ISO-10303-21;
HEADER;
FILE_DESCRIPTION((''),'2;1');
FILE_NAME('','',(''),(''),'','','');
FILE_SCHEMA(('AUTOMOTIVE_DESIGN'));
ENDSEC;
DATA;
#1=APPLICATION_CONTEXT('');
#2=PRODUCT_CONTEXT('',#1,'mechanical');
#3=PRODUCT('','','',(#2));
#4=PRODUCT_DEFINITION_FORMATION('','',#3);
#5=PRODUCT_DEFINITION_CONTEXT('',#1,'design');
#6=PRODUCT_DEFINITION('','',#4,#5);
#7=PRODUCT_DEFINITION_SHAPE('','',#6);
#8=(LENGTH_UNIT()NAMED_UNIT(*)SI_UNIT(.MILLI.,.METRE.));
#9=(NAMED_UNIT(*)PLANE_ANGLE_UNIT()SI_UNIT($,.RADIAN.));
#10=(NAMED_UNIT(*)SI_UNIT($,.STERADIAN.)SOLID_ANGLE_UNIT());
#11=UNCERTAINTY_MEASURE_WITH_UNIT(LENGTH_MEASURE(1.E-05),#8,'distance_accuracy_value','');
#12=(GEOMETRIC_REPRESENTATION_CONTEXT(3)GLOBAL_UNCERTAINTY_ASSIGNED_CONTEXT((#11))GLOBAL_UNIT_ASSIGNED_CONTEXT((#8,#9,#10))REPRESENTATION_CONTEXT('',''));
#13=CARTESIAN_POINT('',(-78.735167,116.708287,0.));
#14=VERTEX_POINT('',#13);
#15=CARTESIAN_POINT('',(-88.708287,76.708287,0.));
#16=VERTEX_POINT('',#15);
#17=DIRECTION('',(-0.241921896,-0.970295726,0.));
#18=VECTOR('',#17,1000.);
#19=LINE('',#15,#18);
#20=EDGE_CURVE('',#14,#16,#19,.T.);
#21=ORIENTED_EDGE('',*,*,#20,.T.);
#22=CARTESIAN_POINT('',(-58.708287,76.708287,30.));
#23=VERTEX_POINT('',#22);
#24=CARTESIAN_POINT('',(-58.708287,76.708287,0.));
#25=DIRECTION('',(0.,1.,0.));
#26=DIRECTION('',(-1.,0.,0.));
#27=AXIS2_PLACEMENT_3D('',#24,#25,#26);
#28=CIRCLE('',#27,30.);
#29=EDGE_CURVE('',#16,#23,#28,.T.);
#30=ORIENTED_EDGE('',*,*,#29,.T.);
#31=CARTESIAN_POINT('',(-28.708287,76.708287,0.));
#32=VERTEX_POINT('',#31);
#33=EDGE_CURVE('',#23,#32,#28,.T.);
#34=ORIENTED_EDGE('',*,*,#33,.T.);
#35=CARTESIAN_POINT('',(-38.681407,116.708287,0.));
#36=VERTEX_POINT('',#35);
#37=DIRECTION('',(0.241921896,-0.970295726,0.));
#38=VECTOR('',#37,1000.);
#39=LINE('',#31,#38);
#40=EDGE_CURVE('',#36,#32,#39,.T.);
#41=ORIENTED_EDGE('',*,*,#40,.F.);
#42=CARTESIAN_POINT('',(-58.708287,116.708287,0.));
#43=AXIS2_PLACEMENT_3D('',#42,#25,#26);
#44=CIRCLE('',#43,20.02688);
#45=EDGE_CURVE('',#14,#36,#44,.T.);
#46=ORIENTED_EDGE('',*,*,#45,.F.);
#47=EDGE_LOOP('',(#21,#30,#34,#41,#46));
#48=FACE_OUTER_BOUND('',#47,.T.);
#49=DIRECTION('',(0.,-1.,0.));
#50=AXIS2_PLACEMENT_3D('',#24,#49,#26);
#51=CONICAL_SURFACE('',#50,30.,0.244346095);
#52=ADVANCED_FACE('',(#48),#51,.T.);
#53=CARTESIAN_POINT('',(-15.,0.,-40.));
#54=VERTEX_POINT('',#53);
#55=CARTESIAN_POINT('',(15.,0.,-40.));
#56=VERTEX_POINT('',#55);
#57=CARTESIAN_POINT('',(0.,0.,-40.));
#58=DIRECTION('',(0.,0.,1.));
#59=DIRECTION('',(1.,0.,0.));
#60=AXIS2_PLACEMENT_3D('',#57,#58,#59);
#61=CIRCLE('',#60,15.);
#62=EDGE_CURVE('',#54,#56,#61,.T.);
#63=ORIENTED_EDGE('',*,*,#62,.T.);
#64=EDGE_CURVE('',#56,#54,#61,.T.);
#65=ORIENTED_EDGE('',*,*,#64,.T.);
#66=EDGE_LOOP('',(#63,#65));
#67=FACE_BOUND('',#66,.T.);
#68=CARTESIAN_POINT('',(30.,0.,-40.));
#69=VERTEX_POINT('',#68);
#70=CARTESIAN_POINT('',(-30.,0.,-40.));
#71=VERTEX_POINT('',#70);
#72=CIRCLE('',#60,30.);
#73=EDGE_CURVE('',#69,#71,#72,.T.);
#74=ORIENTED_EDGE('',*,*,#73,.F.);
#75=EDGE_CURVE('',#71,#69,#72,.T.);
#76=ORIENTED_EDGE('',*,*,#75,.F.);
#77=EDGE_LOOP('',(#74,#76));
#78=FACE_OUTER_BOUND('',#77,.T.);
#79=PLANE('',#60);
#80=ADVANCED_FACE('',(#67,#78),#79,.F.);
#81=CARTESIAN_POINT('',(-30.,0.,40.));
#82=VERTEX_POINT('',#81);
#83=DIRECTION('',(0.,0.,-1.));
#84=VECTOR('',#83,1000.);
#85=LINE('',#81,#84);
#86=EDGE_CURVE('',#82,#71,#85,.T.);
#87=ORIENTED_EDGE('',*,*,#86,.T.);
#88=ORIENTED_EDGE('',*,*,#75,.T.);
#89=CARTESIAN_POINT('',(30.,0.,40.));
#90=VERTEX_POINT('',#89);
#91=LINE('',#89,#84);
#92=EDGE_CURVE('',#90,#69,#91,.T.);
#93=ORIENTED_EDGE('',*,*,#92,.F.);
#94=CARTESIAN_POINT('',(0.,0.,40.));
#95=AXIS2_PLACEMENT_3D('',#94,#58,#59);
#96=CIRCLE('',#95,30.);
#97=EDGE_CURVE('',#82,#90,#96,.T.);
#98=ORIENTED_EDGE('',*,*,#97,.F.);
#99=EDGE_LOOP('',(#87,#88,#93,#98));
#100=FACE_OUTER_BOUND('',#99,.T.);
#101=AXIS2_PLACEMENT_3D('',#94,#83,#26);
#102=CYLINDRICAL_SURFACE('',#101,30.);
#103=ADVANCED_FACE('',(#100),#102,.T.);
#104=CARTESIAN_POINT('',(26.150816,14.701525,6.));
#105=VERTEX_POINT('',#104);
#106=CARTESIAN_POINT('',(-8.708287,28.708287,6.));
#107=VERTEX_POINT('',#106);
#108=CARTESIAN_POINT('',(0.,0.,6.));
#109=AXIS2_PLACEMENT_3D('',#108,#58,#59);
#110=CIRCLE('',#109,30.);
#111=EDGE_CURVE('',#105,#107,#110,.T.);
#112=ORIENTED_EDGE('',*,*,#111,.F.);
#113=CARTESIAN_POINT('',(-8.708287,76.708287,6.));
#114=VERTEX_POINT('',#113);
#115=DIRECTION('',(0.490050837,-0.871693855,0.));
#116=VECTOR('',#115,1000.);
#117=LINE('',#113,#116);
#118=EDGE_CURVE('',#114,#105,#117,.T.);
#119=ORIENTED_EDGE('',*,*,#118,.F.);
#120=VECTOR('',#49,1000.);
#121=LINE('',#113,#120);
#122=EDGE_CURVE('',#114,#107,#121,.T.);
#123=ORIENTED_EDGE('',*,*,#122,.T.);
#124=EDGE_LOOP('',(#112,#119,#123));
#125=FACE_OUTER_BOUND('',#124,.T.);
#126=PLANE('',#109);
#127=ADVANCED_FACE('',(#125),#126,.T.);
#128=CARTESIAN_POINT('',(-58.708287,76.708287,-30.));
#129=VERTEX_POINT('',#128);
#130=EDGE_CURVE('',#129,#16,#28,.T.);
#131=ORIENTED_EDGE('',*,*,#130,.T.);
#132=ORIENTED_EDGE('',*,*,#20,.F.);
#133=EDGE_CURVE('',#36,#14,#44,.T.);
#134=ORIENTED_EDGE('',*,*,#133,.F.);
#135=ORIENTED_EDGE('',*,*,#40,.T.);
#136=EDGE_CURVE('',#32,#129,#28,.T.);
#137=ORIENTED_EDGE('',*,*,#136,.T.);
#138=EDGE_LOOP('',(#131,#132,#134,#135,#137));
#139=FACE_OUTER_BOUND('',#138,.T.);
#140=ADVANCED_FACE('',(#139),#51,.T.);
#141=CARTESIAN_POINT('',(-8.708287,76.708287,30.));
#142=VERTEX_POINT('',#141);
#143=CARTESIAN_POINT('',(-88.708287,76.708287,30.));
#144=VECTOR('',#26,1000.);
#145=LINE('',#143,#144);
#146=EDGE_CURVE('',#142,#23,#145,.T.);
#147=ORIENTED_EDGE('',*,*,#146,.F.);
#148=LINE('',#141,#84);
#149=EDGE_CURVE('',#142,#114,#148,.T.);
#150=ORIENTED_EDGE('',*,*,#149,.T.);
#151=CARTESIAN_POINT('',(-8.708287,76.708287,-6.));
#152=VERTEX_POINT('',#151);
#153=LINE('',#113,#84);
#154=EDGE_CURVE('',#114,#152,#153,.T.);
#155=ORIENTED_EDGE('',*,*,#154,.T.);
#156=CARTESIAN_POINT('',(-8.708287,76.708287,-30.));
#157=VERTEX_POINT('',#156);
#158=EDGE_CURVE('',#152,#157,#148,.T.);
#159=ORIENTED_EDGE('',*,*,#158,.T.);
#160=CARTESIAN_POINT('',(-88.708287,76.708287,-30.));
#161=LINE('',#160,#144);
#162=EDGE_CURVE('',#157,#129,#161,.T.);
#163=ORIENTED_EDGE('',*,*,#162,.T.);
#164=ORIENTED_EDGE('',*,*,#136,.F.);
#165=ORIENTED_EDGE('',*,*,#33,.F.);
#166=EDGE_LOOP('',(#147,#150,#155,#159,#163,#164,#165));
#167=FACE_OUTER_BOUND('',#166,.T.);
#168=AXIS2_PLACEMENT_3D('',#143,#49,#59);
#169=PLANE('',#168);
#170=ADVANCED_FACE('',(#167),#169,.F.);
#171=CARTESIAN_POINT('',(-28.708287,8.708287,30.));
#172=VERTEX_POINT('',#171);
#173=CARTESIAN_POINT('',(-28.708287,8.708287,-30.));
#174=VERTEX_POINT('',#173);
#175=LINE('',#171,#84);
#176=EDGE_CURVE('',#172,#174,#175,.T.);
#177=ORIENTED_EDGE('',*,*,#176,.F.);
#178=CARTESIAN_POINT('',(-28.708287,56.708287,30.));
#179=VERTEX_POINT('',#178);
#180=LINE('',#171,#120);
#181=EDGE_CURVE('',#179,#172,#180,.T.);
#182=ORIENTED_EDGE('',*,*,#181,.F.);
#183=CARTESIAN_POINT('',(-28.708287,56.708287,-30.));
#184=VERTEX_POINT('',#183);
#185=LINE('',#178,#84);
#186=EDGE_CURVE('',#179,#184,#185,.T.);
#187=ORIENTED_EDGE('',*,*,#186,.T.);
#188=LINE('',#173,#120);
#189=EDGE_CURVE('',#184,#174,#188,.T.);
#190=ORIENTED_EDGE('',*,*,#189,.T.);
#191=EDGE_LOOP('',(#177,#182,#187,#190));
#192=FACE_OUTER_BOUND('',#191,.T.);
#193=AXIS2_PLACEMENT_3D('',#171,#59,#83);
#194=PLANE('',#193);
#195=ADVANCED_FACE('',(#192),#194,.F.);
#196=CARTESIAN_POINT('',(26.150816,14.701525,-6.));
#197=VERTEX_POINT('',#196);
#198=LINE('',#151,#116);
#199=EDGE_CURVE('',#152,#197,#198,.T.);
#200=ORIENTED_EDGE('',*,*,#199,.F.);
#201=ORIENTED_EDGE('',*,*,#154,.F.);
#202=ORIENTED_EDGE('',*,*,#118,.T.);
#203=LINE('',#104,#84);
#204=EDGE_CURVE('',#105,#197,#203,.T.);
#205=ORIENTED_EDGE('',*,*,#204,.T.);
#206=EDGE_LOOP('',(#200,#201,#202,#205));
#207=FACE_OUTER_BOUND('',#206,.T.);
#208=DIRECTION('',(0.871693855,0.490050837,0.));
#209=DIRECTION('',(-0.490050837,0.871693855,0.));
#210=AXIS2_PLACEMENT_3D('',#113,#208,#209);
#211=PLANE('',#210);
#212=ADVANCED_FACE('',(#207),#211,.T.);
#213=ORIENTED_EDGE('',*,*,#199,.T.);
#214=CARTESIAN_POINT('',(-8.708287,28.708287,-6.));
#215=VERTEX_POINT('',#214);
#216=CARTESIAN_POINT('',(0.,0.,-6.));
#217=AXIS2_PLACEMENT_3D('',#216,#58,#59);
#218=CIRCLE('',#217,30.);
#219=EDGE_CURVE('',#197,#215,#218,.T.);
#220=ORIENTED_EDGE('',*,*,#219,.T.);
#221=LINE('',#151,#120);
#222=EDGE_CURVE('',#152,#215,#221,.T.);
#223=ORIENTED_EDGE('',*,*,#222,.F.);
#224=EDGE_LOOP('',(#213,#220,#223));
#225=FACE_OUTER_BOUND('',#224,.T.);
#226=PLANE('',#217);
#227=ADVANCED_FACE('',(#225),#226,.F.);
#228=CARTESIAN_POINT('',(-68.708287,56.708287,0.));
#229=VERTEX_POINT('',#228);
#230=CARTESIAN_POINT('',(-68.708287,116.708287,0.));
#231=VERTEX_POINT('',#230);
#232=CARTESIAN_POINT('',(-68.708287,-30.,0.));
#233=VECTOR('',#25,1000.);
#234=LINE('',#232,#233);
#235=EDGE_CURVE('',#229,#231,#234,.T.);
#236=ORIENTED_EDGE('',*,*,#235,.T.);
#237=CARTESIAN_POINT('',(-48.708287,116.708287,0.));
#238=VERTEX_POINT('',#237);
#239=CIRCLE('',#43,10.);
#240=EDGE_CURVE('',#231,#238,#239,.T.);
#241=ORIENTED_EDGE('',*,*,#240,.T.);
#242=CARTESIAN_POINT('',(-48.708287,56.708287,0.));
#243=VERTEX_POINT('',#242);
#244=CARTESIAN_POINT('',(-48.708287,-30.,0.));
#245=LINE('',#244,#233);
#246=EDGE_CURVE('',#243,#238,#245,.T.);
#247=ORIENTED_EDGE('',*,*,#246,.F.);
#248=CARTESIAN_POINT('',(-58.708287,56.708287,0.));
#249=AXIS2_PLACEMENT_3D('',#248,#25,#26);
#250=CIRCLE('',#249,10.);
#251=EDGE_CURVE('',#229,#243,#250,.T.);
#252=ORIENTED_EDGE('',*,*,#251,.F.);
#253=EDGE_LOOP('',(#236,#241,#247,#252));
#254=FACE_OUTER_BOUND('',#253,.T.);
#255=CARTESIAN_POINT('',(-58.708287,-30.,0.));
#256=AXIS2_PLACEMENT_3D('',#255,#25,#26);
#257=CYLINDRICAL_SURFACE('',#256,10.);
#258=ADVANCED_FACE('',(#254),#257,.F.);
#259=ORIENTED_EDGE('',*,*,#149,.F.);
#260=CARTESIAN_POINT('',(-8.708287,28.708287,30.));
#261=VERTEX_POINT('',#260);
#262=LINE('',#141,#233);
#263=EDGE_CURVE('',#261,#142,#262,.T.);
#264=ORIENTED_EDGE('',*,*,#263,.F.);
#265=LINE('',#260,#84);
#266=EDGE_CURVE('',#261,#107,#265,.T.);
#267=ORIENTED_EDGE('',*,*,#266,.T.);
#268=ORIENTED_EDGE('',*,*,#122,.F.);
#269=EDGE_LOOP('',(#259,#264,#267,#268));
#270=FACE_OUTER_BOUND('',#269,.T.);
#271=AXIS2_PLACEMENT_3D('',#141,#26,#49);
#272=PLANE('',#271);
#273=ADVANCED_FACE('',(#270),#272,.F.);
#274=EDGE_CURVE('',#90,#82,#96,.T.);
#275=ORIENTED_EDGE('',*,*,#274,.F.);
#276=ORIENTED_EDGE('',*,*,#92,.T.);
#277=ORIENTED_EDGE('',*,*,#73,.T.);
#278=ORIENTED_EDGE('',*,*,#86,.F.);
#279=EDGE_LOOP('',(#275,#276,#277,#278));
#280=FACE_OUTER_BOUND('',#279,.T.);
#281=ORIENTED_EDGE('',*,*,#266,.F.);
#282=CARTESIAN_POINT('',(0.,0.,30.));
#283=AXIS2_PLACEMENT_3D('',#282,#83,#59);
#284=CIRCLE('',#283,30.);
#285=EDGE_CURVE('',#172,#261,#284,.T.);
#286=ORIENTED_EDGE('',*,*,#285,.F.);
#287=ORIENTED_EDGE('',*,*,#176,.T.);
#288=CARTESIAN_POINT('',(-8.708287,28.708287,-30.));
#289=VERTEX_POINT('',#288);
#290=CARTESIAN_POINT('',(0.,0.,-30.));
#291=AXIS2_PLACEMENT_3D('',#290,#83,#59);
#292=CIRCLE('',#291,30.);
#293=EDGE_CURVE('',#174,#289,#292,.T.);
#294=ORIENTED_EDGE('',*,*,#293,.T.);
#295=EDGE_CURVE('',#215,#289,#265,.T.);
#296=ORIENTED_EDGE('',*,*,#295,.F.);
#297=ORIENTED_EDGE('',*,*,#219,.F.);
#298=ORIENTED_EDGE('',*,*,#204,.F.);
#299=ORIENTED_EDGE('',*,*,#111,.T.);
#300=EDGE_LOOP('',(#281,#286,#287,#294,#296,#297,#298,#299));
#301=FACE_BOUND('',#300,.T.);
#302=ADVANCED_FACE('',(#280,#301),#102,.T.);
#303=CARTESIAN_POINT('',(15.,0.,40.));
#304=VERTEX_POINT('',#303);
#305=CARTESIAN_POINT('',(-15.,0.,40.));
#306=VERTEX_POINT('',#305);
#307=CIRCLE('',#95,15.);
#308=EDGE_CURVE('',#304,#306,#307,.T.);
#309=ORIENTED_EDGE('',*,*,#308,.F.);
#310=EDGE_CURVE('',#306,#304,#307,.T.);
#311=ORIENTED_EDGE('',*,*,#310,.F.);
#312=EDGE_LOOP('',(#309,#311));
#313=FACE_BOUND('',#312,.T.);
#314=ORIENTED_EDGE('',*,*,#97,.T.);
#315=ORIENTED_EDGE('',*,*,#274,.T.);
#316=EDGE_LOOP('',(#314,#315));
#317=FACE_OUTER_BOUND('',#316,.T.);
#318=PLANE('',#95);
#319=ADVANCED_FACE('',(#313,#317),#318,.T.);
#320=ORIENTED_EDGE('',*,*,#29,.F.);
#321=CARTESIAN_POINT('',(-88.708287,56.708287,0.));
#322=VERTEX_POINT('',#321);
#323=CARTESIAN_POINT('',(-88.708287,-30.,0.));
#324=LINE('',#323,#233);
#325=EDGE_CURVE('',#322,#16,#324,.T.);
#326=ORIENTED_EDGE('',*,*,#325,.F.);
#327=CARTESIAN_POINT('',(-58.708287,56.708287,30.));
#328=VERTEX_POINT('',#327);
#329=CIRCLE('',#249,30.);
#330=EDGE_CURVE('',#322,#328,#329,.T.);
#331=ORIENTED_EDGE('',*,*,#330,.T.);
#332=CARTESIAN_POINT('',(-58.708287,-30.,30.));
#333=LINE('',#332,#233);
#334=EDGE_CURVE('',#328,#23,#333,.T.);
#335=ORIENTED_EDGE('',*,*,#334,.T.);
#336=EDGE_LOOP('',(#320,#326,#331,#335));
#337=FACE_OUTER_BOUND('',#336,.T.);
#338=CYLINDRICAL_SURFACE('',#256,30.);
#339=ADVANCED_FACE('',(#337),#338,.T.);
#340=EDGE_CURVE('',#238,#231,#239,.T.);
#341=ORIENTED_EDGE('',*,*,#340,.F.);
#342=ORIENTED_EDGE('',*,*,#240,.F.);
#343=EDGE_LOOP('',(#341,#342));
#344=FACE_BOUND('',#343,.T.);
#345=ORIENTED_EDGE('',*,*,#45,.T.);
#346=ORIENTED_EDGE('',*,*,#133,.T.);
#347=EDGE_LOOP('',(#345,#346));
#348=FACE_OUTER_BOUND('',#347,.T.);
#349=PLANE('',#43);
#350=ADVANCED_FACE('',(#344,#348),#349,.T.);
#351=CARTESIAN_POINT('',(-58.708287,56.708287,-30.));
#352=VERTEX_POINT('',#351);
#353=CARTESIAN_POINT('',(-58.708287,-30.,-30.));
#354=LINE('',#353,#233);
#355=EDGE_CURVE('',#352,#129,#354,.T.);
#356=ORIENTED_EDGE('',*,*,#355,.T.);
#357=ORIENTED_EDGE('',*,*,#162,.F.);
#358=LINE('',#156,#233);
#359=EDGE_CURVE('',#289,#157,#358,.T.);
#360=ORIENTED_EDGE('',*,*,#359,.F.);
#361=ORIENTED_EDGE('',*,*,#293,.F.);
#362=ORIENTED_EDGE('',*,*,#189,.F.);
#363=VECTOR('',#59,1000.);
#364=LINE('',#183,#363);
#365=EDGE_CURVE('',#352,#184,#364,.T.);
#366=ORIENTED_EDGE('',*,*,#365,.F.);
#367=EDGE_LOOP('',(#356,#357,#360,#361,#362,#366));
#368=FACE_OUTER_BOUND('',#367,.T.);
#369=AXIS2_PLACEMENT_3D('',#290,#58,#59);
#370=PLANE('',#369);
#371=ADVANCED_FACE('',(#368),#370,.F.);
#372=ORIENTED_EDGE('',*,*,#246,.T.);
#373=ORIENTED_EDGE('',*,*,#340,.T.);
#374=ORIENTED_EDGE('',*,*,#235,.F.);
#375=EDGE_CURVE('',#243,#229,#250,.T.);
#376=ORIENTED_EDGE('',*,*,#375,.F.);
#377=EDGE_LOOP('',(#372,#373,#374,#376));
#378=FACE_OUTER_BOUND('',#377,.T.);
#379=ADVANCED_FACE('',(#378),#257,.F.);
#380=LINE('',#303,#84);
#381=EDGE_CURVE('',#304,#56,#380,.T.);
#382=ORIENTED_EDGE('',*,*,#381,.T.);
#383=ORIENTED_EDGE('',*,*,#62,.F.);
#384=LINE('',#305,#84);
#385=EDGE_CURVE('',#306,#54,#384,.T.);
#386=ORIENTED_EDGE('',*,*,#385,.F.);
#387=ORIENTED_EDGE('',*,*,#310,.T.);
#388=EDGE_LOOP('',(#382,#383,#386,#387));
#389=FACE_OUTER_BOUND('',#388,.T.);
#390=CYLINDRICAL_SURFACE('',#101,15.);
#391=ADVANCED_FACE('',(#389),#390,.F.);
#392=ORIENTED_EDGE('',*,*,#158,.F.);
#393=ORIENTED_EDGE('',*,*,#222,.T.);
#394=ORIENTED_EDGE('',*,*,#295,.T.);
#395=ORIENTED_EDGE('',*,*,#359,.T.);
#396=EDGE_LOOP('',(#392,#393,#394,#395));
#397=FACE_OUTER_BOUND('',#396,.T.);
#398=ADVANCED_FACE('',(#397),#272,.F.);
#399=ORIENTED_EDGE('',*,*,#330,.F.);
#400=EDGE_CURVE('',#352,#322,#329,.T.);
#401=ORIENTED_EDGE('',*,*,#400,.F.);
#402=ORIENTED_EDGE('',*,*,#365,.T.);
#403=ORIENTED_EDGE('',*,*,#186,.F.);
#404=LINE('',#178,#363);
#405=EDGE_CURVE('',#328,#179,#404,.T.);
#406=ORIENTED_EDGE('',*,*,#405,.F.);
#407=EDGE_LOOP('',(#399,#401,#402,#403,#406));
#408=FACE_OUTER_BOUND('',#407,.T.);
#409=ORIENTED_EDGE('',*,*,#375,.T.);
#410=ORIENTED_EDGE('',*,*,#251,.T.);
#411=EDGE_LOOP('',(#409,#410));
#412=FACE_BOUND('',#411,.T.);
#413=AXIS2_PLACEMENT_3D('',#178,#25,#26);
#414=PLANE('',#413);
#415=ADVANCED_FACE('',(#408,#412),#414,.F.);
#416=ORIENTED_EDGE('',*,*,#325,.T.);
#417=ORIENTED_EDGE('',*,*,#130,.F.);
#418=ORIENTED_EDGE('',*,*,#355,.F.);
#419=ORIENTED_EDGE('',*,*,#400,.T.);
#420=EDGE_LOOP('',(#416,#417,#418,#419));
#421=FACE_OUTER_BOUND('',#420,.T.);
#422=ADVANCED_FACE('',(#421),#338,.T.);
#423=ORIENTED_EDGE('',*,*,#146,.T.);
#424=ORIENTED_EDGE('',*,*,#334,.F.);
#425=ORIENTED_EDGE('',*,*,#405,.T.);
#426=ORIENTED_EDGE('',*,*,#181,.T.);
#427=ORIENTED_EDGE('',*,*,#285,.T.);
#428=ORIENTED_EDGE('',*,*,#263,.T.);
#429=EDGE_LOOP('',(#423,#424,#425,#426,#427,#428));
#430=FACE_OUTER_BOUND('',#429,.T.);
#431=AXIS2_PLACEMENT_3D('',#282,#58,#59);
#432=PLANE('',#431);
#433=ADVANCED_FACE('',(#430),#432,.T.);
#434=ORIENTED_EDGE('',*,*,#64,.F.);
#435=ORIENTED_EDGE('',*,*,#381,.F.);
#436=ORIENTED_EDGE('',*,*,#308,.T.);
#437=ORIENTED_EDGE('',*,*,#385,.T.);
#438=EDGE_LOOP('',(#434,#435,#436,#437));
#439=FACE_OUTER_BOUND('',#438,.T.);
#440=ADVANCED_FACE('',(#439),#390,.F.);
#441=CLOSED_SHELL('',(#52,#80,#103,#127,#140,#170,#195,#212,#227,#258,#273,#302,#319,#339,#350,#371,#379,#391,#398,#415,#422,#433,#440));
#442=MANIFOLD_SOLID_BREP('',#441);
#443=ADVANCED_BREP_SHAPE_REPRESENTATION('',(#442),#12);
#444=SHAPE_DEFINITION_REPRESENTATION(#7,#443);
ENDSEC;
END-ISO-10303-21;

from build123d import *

# Parameters (mm, degrees)
BASE_BLOCK_SKETCH_R            = 30
BASE_BLOCK_SKETCH_R_2          = 15
BASE_BLOCK_DEPTH               = 40
ARM_DEPTH                      = 30
SUPPORT_RIB_DEPTH              = 6
PROFILE_CUT_DEPTH              = 145.415437787
DRAFTED_BOSS_SKETCH_R          = 30
DRAFTED_CYLINDRICAL_BOSS_DEPTH = 40
DRAFTED_CYLINDRICAL_BOSS_TAPER = 14
BOSS_BORE_SKETCH_R             = 10
BOSS_BORE_20_DEPTH             = 177.046816624


with BuildPart() as part:
    # Base Block Sketch → Base Block (new, symmetric)
    with BuildSketch(Plane.XY):
        Circle(BASE_BLOCK_SKETCH_R)
        Circle(BASE_BLOCK_SKETCH_R_2, mode=Mode.SUBTRACT)
    extrude(amount=BASE_BLOCK_DEPTH, both=True)

    # Arm Profile Sketch → Arm (add, symmetric)
    with BuildSketch(Plane.XY):
        with BuildLine():
            Line((-28.708286934, 8.708286934), (-28.708286934, 56.708286934))
            Line((-28.708286934, 56.708286934), (-88.708286934, 56.708286934))
            Line((-88.708286934, 56.708286934), (-88.708286934, 76.708286934))
            Line((-88.708286934, 76.708286934), (-8.708286934, 76.708286934))
            Line((-8.708286934, 76.708286934), (-8.708286934, 28.708286934))
            ThreePointArc((-8.708286934, 28.708286934), (-21.213203436, 21.213203436), (-28.708286934, 8.708286934))
        make_face()
    extrude(amount=ARM_DEPTH, both=True)

    # Support Rib Sketch → Support Rib (add, symmetric)
    with BuildSketch(Plane.XY):
        with BuildLine():
            Line((-8.708286934, 76.708286934), (26.150815657, 14.701525107))
            ThreePointArc((26.150815657, 14.701525107), (11.185159645, 27.836885668), (-8.708286934, 28.708286934))
            Line((-8.708286934, 28.708286934), (-8.708286934, 76.708286934))
        make_face()
    extrude(amount=SUPPORT_RIB_DEPTH, both=True)

    # Profile Cut Sketch → Profile Cut (cut, through all)
    with BuildSketch(Plane(origin=(0, 76.708286934, 0), x_dir=(1, 0, 0), z_dir=(0, 1, 0))):
        with BuildLine():
            Line((-88.708286934, -30), (-58.708286934, -30))
            ThreePointArc((-58.708286934, -30), (-79.921490369, -21.213203436), (-88.708286934, 0))
            Line((-88.708286934, 0), (-88.708286934, -30))
        make_face()
        with BuildLine():
            ThreePointArc((-88.708286934, 0), (-79.921490369, 21.213203436), (-58.708286934, 30))
            Line((-58.708286934, 30), (-88.708286934, 30))
            Line((-88.708286934, 30), (-88.708286934, 0))
        make_face()
    extrude(amount=-PROFILE_CUT_DEPTH, mode=Mode.SUBTRACT)

    # Drafted Boss Sketch → Drafted Cylindrical Boss (add)
    with BuildSketch(Plane(origin=(0, 76.708286934, 0), x_dir=(1, 0, 0), z_dir=(0, 1, 0))):
        with Locations((-58.708286934, 0)):
            Circle(DRAFTED_BOSS_SKETCH_R)
    extrude(amount=DRAFTED_CYLINDRICAL_BOSS_DEPTH, taper=DRAFTED_CYLINDRICAL_BOSS_TAPER)

    # Boss Bore Sketch → Boss Bore Ø20 (cut, through all)
    with BuildSketch(Plane(origin=(0, 116.708286934, 0), x_dir=(1, 0, 0), z_dir=(0, 1, 0))):
        with Locations(Location((-58.708286934, 0, 0), (0, 0, 180))):
            Circle(BOSS_BORE_SKETCH_R)
    extrude(amount=-BOSS_BORE_20_DEPTH, mode=Mode.SUBTRACT)


solid = part.part
